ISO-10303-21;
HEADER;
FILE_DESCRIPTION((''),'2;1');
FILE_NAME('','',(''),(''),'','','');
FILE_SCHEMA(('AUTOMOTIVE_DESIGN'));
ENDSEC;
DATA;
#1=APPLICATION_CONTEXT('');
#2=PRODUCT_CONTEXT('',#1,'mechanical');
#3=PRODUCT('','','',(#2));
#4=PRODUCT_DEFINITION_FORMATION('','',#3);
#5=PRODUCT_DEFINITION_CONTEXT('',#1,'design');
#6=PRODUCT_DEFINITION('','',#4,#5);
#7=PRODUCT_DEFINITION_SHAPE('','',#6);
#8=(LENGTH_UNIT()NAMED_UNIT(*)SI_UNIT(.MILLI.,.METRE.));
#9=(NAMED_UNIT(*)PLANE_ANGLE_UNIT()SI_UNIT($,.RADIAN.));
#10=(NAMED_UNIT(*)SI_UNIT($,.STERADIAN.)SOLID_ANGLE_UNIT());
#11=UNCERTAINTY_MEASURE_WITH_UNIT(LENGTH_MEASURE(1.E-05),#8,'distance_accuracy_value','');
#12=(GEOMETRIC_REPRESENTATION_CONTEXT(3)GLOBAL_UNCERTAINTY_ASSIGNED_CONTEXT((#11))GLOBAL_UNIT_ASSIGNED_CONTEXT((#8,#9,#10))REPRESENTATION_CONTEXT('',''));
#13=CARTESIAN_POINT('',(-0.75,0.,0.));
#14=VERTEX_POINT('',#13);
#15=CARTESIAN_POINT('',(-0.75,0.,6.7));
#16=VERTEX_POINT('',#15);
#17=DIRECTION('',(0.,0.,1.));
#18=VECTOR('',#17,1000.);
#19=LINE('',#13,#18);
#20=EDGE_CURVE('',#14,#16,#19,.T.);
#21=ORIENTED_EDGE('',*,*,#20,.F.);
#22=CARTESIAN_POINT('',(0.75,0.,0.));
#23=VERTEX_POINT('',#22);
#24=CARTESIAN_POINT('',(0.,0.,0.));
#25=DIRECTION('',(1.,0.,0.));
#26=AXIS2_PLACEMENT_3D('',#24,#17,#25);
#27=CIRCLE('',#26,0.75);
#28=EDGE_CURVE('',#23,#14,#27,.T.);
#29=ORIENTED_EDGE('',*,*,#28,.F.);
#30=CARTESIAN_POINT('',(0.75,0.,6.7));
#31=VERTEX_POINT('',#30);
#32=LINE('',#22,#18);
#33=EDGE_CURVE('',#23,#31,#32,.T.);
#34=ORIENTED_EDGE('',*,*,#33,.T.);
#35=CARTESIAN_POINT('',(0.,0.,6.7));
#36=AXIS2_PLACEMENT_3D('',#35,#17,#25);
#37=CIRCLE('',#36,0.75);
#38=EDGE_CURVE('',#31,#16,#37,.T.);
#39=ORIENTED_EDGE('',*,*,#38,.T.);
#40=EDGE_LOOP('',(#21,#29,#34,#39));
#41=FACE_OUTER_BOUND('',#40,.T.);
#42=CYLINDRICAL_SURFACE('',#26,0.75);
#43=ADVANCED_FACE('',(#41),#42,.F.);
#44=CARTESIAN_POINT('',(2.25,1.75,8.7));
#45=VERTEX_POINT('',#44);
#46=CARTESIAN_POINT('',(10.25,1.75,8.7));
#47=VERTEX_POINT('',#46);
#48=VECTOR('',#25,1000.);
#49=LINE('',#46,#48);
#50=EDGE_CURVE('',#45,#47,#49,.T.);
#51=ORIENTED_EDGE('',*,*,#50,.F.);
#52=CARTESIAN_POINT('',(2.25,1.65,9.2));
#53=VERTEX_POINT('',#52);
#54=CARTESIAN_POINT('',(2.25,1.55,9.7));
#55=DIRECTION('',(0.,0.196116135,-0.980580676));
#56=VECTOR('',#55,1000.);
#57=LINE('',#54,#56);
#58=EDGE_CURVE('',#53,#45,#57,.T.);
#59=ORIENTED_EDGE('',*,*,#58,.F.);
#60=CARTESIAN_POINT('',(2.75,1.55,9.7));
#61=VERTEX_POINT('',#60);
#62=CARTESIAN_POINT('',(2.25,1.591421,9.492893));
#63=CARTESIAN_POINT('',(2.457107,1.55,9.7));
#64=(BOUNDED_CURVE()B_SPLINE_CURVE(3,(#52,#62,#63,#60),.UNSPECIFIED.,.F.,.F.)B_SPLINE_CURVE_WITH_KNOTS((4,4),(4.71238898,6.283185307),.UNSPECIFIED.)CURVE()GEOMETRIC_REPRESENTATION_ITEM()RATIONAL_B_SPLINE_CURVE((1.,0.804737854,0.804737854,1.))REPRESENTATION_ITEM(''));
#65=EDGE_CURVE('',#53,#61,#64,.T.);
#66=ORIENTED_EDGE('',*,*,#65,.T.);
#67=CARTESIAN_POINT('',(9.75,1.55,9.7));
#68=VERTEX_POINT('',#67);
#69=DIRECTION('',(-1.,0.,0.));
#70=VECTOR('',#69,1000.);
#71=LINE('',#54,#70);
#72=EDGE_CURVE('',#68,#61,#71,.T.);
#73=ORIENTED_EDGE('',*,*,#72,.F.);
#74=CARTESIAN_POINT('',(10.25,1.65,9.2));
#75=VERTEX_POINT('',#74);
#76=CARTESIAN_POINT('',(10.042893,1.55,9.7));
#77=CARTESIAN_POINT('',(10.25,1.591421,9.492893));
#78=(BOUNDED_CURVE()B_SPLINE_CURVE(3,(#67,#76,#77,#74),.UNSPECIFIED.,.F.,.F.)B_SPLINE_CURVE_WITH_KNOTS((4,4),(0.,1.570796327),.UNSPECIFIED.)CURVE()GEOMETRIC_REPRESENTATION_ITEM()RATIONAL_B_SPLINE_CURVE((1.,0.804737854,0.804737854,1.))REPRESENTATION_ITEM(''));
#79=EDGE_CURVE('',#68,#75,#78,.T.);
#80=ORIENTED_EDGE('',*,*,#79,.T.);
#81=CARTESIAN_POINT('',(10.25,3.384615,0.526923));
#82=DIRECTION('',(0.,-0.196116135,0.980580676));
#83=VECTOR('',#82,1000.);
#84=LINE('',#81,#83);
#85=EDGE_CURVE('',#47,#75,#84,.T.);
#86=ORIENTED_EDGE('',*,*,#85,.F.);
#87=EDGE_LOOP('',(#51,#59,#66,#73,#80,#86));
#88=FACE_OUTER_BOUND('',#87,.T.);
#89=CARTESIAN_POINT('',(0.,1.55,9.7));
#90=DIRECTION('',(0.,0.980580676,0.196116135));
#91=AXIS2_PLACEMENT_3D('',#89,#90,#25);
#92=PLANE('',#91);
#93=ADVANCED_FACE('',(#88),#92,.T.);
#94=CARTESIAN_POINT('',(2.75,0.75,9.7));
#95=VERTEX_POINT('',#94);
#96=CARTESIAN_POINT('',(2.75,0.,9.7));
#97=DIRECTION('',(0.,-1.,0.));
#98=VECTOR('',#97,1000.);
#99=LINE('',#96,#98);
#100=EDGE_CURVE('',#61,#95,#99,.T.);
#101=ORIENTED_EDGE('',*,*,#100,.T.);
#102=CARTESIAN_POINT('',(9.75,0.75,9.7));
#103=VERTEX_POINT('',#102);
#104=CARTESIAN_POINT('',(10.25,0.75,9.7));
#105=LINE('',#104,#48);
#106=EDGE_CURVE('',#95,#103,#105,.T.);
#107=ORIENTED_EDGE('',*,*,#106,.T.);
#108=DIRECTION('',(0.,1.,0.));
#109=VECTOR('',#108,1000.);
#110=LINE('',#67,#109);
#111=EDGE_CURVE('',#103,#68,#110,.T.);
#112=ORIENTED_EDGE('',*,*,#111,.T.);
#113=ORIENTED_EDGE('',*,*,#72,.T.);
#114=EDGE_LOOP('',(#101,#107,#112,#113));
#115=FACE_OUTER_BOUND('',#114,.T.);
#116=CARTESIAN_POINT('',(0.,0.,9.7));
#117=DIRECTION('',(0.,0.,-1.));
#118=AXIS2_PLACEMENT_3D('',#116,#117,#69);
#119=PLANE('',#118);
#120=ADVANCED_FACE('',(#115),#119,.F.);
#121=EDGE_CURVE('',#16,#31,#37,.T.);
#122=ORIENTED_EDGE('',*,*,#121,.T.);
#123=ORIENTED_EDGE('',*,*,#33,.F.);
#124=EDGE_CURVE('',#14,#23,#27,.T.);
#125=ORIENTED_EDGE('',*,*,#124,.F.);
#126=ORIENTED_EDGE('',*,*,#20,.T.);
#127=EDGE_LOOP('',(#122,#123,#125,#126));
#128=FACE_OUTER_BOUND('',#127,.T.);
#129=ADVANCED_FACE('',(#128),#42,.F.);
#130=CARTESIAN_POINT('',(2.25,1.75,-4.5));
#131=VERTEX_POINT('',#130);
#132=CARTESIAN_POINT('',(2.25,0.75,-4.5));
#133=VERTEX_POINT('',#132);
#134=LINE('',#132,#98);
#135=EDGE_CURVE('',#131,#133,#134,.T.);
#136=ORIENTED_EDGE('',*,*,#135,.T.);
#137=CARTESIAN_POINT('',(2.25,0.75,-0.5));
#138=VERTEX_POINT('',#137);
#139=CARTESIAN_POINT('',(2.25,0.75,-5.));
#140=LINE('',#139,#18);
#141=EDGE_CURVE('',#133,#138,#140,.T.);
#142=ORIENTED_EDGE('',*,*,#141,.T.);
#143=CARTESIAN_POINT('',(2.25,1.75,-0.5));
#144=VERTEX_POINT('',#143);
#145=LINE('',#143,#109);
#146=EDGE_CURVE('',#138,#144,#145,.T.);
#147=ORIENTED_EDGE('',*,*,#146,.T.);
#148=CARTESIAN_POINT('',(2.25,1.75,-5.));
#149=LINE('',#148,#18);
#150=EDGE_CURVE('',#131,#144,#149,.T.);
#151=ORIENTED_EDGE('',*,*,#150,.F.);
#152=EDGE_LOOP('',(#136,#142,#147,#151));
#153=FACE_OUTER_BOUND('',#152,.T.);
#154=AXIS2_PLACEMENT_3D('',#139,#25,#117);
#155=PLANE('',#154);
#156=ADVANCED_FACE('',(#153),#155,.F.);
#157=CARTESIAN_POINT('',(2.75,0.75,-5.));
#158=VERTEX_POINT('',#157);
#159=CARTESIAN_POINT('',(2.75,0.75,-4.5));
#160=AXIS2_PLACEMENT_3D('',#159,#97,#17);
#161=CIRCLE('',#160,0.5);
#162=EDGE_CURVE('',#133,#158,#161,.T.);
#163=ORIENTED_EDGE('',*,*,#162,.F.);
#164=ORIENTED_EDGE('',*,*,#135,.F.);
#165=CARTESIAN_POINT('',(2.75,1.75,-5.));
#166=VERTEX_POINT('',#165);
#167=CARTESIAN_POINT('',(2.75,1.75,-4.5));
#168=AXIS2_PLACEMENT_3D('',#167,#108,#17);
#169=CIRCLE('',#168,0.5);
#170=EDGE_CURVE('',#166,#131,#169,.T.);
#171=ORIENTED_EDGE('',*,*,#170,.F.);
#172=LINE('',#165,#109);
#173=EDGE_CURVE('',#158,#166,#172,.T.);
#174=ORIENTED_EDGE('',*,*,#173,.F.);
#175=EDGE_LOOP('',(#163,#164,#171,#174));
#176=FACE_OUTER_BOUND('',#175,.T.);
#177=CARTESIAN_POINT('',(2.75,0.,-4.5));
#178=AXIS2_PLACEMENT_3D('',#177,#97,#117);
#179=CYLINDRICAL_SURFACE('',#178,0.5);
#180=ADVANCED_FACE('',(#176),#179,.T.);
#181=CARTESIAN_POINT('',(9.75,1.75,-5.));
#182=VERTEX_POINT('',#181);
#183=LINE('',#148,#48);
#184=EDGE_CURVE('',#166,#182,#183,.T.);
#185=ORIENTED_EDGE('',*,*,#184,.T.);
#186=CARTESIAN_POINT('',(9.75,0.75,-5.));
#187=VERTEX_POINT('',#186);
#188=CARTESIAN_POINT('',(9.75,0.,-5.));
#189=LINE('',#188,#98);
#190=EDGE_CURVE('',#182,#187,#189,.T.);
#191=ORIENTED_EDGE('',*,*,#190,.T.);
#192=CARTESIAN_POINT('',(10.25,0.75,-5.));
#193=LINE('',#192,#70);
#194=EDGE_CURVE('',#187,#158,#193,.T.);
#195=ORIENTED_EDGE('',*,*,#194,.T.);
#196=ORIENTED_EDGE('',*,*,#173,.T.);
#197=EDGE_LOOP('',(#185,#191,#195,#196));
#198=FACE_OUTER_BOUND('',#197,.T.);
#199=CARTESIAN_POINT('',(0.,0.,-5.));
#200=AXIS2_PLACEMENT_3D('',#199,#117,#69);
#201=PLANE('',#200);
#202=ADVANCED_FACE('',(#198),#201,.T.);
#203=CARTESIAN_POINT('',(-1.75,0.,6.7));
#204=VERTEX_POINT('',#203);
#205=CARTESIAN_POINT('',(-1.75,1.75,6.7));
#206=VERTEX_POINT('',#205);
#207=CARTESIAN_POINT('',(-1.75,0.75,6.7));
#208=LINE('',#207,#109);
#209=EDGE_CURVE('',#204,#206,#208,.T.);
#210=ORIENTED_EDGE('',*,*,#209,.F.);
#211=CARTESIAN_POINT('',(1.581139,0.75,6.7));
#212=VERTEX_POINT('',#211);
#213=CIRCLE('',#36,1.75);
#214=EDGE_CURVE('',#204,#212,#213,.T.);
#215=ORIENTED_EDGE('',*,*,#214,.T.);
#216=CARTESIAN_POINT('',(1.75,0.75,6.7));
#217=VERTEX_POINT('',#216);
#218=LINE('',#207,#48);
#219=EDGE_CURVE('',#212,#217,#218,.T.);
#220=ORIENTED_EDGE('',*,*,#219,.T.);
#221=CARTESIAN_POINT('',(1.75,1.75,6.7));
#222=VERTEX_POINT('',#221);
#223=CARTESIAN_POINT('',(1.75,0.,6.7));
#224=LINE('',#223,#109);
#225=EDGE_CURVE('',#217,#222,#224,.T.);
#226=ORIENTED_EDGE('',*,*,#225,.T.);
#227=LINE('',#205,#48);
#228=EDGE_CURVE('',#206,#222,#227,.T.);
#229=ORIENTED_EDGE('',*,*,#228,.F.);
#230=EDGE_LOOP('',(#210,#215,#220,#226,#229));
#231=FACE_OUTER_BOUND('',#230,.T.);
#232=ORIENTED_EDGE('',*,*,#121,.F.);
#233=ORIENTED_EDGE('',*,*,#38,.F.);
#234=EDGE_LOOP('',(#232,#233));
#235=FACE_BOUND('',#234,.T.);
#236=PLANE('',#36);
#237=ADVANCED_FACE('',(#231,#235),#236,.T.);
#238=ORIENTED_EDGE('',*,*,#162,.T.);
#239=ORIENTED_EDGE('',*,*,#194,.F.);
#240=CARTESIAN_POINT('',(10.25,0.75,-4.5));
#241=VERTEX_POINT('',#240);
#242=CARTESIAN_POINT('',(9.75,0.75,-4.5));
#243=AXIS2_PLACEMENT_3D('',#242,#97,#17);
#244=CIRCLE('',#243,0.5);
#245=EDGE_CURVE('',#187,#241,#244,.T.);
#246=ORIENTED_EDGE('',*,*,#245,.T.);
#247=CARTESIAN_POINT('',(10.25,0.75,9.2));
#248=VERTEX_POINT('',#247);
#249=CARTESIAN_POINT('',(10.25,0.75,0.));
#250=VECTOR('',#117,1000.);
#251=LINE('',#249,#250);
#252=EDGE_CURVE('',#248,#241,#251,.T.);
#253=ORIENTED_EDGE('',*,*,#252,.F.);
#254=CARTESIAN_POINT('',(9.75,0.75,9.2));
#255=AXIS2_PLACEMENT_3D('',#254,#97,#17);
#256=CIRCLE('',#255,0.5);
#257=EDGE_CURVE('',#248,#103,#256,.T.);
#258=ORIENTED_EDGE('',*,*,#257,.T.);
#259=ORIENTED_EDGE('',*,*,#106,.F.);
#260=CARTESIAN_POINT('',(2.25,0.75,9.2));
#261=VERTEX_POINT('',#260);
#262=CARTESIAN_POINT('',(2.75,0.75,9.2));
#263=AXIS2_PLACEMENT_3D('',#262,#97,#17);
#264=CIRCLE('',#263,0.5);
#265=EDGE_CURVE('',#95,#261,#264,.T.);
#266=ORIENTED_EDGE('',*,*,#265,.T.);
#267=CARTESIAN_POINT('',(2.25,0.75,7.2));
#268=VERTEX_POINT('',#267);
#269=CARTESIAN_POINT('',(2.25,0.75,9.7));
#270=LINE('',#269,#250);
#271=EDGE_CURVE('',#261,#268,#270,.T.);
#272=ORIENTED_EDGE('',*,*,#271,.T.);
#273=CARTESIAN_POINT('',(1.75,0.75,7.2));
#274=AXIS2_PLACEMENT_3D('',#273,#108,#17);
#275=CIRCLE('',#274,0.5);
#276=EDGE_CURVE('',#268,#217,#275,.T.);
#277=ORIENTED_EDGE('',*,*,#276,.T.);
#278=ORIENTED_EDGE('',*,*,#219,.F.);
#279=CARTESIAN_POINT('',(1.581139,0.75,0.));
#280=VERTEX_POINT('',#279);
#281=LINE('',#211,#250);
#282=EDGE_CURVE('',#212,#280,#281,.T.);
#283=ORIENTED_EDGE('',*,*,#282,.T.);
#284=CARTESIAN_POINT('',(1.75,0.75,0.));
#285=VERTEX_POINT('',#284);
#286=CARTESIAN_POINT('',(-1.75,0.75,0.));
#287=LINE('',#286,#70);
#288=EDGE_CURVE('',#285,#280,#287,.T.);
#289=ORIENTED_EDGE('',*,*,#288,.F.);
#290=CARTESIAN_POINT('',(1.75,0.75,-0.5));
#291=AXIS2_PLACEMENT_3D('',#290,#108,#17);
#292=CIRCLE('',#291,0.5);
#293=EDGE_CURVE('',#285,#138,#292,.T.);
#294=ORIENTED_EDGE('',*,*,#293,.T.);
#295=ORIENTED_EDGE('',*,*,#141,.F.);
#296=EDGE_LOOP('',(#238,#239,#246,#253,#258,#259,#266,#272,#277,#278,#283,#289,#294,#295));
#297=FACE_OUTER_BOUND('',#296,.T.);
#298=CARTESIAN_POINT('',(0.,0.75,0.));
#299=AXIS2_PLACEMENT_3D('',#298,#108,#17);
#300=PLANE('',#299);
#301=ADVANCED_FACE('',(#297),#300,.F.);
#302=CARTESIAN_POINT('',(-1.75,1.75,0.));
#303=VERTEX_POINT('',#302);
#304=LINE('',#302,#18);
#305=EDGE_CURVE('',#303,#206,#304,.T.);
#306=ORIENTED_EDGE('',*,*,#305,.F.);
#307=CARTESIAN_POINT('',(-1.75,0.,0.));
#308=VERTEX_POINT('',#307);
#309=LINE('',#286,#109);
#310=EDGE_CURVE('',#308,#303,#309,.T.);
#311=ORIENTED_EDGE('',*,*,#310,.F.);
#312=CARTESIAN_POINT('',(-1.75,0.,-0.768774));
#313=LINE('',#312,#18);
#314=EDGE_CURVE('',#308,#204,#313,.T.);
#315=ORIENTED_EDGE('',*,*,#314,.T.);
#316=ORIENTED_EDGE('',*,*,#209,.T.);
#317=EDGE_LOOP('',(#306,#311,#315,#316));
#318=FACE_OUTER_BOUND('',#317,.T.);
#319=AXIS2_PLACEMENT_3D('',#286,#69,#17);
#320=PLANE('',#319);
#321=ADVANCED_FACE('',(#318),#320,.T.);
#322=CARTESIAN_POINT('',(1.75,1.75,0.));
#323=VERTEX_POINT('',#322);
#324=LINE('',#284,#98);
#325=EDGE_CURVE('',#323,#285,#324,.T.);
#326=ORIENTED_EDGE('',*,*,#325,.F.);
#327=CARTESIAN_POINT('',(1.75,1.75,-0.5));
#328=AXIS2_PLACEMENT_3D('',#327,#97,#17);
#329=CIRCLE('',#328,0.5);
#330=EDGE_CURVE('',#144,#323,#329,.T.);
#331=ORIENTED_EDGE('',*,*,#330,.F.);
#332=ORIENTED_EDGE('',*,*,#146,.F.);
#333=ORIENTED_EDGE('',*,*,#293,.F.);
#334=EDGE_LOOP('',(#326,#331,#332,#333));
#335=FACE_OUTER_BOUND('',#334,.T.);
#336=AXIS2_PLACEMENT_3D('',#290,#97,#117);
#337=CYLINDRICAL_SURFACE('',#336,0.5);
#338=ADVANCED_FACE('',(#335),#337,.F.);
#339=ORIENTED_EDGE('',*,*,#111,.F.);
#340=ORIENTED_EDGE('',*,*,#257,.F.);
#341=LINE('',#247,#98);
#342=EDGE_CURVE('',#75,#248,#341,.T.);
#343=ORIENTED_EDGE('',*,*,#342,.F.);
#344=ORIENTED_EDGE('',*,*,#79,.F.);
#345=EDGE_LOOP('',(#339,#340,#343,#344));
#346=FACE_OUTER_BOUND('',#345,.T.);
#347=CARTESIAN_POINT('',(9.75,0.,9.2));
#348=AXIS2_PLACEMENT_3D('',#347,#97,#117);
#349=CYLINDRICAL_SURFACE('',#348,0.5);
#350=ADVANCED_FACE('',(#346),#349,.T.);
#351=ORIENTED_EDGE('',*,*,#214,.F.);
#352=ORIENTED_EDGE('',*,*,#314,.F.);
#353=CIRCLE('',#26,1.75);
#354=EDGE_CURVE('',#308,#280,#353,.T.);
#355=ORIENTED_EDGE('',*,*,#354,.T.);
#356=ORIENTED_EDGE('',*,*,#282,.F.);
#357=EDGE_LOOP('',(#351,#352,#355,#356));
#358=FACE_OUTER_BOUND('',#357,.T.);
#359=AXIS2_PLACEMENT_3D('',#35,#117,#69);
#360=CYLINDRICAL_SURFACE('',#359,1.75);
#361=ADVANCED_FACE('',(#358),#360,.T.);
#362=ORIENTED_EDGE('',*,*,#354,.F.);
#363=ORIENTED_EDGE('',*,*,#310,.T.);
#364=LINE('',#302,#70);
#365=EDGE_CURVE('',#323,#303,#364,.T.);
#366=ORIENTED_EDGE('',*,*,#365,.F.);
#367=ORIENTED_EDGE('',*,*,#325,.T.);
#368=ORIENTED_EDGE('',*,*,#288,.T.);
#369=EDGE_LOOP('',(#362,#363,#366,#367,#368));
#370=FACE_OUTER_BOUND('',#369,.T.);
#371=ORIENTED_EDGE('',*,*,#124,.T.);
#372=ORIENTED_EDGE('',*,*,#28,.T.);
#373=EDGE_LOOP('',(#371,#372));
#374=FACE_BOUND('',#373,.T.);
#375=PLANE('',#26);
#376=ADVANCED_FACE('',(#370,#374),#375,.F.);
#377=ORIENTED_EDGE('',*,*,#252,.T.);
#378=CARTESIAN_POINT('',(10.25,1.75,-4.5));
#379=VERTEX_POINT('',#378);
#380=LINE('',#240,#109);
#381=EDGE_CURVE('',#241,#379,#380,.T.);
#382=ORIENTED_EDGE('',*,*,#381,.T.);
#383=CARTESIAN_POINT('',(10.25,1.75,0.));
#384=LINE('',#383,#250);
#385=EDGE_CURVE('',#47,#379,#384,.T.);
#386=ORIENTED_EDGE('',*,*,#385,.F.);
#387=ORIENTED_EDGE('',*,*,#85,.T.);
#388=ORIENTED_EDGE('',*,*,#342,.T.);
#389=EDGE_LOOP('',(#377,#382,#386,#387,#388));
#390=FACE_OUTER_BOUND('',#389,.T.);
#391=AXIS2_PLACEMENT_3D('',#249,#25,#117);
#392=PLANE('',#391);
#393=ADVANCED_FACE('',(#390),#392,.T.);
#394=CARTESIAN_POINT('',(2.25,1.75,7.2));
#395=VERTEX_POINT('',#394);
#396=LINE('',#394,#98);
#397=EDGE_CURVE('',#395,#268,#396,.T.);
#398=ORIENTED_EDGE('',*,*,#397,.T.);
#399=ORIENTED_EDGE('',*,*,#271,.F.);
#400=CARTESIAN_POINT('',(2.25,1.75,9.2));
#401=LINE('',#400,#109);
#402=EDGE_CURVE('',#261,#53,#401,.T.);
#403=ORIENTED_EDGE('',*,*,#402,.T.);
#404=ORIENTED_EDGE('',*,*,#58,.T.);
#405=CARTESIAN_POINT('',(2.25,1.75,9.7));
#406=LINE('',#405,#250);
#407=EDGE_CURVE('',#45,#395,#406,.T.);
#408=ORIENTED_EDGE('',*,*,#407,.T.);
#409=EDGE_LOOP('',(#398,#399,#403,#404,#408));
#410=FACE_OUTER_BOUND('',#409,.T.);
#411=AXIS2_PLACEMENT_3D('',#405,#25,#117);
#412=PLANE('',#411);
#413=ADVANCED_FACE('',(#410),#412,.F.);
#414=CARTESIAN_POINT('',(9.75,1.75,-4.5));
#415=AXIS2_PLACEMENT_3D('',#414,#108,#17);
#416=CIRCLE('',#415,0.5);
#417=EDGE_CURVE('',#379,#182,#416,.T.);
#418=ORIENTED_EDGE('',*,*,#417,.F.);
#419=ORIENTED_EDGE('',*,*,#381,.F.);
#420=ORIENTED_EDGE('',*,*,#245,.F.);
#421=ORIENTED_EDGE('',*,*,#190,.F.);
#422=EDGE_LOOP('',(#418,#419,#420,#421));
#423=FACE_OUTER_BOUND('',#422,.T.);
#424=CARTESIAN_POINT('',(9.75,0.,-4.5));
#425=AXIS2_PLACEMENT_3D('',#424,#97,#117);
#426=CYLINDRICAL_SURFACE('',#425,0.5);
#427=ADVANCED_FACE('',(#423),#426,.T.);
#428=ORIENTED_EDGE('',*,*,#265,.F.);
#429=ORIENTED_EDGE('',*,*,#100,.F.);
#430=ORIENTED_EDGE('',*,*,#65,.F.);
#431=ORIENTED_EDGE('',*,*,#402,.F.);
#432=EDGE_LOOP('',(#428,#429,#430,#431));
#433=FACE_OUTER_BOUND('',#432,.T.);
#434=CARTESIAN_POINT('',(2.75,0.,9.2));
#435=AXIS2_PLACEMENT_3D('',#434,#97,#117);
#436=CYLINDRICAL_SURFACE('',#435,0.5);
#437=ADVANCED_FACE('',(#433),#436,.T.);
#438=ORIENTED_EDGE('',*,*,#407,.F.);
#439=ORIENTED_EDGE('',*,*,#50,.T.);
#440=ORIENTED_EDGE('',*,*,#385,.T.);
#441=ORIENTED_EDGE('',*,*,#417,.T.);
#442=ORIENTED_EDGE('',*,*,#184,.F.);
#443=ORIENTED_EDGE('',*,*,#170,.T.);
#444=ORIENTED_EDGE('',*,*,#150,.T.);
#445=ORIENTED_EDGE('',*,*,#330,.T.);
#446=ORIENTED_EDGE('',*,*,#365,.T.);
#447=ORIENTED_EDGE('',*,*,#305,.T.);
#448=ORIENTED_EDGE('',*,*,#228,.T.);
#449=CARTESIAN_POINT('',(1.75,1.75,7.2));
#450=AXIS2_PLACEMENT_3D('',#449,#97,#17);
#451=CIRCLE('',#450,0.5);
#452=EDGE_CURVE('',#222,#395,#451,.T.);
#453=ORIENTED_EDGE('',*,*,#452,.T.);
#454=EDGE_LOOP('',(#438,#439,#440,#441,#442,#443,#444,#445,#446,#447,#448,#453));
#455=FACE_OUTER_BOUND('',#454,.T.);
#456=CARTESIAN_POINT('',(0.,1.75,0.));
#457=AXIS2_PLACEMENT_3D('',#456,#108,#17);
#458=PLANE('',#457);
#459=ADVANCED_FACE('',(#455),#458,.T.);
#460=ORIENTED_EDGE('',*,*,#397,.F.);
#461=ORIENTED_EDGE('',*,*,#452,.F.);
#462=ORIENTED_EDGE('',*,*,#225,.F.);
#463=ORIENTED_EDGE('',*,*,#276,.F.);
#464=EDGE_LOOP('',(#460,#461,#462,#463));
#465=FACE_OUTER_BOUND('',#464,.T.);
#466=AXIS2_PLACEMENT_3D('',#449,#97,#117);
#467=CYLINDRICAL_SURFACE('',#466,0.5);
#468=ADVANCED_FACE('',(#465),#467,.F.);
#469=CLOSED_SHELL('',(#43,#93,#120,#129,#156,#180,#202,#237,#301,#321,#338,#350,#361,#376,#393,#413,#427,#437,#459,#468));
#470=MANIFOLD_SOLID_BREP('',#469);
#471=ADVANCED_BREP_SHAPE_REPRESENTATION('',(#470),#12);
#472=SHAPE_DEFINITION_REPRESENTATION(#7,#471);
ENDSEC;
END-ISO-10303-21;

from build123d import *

# Parameters (mm, degrees)
SKETCH1_R           = 1.75
BOSS_EXTRUDE1_DEPTH = 6.7
SKETCH2_R           = 0.75
CUT_EXTRUDE1_DEPTH  = 8.142478561
SKETCH3_W           = 12
SKETCH3_H           = 6.7
BOSS_EXTRUDE2_DEPTH = 1
BOSS_EXTRUDE3_START = -6.7
BOSS_EXTRUDE3_DEPTH = 6.7
SKETCH5_W           = 8
SKETCH5_H           = 1
BOSS_EXTRUDE4_DEPTH = 3
SKETCH6_W           = 8
SKETCH6_H           = 1
BOSS_EXTRUDE5_DEPTH = 5
CHAMFER1_SIZE       = 1
CHAMFER1_SIZE2      = 0.2
FILLET1_R           = 0.5


with BuildPart() as part:
    # Sketch1 → Boss-Extrude1 (new body)
    with BuildSketch(Plane.XY):
        Circle(SKETCH1_R)
    extrude(amount=BOSS_EXTRUDE1_DEPTH)

    # Sketch2 → Cut-Extrude1 (cut, through all)
    with BuildSketch(Plane.XY.offset(6.7)):
        Circle(SKETCH2_R)
    extrude(amount=-CUT_EXTRUDE1_DEPTH, mode=Mode.SUBTRACT)

    # Sketch3 → Boss-Extrude2 (add)
    with BuildSketch(Plane(origin=(0, 1.75, 0), x_dir=(1, 0, 0), z_dir=(0, 1, 0))):
        with Locations((4.25, -3.35)):
            Rectangle(SKETCH3_W, SKETCH3_H)
    extrude(amount=-BOSS_EXTRUDE2_DEPTH)

    # Sketch4 → Boss-Extrude3 (add)
    with BuildSketch(Plane.XY.offset(6.7).offset(BOSS_EXTRUDE3_START)):
        with BuildLine():
            Line((-1.75, 0.75), (-1.75, 0))
            ThreePointArc((-1.75, 0), (-1.707262861, 0.384387205), (-1.58113883, 0.75))
            Line((-1.58113883, 0.75), (-1.75, 0.75))
        make_face()
    extrude(amount=BOSS_EXTRUDE3_DEPTH)

    # Sketch5 → Boss-Extrude4 (add)
    with BuildSketch(Plane.XY.offset(6.7)):
        with Locations((6.25, 1.25)):
            Rectangle(SKETCH5_W, SKETCH5_H)
    extrude(amount=BOSS_EXTRUDE4_DEPTH)

    # Sketch6 → Boss-Extrude5 (add)
    with BuildSketch(Plane(origin=(0, 0, 0), x_dir=(-1, 0, 0), z_dir=(0, 0, -1))):
        with Locations((-6.25, 1.25)):
            Rectangle(SKETCH6_W, SKETCH6_H)
    extrude(amount=BOSS_EXTRUDE5_DEPTH)

    # Chamfer1
    chamfer1_edges = [part.edges().sort_by_distance(p)[0] for p in [
        (6.25, 1.75, 9.7),
    ]]
    chamfer1_side = [part.faces().sort_by_distance(p)[0] for p in [
        (5.136426593, 1.75, 2.535595568),
    ]]
    chamfer(chamfer1_edges, length=CHAMFER1_SIZE, length2=CHAMFER1_SIZE2, reference=chamfer1_side[0])

    # Fillet1
    fillet1_edges = [part.edges().sort_by_distance(p)[0] for p in [
        (2.25, 1.25, 6.7),
        (10.25, 1.15, 9.7),
        (2.25, 1.25, 0),
        (10.25, 1.25, -5),
        (2.25, 1.25, -5),
        (2.25, 1.15, 9.7),
    ]]
    fillet(fillet1_edges, radius=FILLET1_R)


solid = part.part
